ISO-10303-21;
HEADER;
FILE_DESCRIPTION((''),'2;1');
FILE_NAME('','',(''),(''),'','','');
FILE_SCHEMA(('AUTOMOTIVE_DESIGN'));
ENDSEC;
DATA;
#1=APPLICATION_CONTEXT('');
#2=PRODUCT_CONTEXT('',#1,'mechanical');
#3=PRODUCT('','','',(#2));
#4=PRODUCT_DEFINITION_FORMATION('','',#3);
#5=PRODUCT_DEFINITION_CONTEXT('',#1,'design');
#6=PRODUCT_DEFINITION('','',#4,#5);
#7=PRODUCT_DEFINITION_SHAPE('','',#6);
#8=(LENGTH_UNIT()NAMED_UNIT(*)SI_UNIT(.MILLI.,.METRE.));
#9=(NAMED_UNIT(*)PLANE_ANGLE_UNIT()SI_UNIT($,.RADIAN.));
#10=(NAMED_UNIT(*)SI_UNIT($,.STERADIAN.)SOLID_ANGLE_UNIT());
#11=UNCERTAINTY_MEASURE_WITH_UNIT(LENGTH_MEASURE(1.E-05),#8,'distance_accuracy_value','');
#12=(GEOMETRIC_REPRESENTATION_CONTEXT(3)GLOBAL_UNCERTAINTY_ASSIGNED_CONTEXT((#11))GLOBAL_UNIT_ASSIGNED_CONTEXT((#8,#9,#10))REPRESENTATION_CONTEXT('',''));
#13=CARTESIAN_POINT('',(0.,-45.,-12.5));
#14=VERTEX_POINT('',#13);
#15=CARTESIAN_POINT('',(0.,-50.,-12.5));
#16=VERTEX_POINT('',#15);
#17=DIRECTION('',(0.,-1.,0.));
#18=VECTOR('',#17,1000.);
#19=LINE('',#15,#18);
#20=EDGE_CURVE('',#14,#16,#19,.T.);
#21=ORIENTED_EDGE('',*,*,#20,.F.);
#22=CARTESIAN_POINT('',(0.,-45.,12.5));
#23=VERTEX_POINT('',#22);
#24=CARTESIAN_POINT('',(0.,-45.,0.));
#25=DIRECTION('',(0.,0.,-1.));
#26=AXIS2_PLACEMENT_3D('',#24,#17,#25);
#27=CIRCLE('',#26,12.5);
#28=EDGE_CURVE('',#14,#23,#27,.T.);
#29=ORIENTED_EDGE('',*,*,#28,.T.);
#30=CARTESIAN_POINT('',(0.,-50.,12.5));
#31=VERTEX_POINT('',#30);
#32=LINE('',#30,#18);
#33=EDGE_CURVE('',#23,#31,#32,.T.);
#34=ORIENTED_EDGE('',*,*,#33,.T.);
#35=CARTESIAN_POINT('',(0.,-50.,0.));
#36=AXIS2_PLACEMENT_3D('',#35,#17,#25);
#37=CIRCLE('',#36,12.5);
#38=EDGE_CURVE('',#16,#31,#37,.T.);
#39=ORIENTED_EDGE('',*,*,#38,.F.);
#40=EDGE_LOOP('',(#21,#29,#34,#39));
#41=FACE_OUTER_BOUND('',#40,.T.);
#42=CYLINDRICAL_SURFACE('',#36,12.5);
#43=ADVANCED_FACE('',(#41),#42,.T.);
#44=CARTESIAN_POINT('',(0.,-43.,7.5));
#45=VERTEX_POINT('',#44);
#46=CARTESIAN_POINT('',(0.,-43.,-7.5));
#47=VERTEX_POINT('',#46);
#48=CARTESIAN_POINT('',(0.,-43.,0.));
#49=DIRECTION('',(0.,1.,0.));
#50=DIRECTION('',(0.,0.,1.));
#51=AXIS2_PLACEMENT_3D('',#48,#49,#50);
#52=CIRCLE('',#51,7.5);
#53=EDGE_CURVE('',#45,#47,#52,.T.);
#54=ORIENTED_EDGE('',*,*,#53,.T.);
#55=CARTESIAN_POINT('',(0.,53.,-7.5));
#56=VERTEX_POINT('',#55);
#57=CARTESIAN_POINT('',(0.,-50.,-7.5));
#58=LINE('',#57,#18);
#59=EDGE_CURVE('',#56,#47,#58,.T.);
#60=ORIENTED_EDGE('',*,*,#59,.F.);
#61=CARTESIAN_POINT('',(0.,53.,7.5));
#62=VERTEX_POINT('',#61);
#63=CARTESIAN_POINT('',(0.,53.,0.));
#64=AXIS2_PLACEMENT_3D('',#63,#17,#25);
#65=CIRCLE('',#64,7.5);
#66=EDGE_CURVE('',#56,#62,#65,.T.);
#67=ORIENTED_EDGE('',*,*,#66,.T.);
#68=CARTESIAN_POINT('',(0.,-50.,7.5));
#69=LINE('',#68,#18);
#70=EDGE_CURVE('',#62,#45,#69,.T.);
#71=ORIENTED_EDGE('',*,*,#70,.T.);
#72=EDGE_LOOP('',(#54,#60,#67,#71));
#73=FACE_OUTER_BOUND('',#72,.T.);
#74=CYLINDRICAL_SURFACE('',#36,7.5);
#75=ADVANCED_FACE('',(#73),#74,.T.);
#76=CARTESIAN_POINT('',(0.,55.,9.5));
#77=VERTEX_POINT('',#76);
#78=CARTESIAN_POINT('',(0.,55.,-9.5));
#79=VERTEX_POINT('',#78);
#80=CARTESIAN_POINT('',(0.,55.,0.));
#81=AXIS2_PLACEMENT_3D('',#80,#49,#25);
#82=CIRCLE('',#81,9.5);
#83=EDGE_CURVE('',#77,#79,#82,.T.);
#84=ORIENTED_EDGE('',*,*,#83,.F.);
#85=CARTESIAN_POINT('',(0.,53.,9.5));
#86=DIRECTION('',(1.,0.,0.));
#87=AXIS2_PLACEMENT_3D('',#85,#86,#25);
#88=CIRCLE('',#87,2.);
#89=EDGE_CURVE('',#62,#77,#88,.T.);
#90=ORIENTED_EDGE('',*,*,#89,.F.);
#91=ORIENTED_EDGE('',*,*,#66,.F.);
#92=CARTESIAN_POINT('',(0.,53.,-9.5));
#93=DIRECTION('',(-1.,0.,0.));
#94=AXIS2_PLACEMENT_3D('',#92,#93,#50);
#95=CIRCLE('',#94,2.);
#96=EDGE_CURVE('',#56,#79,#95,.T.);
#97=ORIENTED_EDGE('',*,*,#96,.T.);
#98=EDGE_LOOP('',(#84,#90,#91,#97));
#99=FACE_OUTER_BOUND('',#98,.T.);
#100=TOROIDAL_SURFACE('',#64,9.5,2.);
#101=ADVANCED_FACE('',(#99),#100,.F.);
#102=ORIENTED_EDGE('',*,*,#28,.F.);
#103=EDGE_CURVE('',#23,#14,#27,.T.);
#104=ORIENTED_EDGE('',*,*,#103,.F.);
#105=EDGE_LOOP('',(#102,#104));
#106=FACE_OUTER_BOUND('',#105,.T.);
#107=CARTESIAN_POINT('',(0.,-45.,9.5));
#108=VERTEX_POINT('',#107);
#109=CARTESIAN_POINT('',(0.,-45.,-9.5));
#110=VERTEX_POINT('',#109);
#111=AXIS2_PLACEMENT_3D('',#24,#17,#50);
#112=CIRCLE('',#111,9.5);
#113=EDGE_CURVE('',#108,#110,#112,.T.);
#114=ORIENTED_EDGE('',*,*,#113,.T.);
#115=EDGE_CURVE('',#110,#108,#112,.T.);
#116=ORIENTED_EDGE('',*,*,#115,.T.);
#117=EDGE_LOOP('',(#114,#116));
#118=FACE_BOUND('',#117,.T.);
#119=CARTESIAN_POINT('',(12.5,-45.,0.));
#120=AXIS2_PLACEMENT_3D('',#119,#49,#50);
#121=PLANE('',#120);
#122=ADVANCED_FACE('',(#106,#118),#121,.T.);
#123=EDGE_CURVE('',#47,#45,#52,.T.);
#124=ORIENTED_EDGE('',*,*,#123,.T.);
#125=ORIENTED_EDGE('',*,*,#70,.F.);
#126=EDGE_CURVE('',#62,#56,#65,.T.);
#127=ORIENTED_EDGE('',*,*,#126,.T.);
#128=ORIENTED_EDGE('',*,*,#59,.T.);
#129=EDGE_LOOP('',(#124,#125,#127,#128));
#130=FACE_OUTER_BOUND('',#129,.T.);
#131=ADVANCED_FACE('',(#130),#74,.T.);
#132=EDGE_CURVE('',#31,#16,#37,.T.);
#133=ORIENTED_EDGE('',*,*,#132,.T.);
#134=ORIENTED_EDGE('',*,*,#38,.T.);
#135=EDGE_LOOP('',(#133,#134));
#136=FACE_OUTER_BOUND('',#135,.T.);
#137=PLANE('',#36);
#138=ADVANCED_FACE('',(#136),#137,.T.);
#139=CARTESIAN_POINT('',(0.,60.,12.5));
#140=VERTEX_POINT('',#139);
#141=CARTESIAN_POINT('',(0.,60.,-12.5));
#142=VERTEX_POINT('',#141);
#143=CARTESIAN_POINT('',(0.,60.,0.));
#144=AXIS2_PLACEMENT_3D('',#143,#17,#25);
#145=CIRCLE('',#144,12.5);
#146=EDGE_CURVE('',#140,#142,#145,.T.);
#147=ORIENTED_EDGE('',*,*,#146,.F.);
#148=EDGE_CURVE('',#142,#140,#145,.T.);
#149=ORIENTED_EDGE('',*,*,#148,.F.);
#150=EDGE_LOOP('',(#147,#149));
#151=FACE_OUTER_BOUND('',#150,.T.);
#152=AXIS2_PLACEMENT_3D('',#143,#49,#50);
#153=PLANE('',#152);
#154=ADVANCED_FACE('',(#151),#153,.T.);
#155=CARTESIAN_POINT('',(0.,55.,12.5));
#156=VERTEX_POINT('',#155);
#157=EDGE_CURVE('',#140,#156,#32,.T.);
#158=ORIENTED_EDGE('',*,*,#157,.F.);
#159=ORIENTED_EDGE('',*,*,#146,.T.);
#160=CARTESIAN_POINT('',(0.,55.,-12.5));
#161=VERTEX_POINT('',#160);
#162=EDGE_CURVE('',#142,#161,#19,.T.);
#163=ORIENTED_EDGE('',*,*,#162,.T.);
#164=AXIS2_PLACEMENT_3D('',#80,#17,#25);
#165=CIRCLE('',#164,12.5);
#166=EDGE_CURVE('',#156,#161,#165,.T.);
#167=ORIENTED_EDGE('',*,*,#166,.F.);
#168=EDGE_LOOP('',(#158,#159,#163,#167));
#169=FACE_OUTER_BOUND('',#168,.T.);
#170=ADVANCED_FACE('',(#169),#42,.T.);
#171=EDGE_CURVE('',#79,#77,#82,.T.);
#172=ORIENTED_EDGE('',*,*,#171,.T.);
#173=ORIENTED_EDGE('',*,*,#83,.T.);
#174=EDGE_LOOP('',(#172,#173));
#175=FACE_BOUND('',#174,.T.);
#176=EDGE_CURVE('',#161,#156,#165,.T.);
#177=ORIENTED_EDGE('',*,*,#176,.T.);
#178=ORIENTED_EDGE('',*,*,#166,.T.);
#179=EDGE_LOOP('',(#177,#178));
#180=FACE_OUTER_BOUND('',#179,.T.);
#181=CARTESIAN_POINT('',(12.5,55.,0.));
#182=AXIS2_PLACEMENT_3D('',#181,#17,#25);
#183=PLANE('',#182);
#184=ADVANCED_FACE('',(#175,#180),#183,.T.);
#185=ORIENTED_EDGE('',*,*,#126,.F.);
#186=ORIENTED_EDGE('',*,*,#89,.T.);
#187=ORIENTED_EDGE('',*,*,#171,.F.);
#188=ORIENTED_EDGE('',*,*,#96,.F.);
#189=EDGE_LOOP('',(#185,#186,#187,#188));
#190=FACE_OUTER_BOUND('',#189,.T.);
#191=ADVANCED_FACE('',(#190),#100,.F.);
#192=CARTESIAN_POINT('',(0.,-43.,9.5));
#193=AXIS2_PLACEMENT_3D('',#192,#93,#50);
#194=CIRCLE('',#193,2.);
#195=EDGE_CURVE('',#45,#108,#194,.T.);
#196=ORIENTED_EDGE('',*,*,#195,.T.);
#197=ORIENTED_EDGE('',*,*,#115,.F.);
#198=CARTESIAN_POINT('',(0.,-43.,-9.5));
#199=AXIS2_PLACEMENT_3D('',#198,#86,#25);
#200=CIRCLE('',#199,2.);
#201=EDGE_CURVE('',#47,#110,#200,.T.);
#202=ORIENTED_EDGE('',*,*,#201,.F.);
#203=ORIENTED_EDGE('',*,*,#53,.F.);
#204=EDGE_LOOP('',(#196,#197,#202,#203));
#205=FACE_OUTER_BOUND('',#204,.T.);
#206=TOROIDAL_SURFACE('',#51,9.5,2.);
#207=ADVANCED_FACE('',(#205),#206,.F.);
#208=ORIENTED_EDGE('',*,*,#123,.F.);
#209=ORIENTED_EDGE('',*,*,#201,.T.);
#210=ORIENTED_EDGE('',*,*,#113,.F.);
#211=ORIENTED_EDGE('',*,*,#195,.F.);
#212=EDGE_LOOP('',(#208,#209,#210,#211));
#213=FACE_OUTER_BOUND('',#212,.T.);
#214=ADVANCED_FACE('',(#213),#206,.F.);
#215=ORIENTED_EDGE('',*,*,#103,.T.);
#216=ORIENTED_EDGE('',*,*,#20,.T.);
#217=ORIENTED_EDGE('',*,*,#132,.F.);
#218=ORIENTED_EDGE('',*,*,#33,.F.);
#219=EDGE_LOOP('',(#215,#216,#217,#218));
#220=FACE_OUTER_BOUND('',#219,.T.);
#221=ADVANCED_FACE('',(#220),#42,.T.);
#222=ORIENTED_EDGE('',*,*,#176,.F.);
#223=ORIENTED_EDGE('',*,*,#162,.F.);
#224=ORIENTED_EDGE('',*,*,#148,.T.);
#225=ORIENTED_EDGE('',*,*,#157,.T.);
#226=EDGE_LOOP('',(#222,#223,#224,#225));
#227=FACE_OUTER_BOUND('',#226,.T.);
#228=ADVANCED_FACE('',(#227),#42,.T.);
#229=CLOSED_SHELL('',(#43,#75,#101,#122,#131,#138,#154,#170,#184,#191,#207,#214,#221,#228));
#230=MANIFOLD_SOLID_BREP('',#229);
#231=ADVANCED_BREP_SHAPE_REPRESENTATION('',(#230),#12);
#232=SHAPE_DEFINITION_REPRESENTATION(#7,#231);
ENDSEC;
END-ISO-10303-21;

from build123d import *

# Parameters (mm, degrees)
FILLET_1_R = 2


with BuildPart() as part:
    # 草图1 → 旋转2 (revolve)
    with BuildSketch(Plane.XY, mode=Mode.PRIVATE) as revolve_2_sk:
        Polygon((0, -50), (0, 60), (12.5, 60), (12.5, 55), (7.5, 55), (7.5, -45), (12.5, -45), (12.5, -50), align=None)
    revolve(revolve_2_sk.sketch.rotate(Axis((0, -50, 0), (0, 1, 0)), 90), axis=Axis((0, -50, 0), (0, 1, 0)))

    # 圆角1
    fillet_1_edges = [part.edges().sort_by_distance(p)[0] for p in [
        (0, -45, 7.5),
        (0, 55, 7.5),
    ]]
    fillet(fillet_1_edges, radius=FILLET_1_R)


solid = part.part
